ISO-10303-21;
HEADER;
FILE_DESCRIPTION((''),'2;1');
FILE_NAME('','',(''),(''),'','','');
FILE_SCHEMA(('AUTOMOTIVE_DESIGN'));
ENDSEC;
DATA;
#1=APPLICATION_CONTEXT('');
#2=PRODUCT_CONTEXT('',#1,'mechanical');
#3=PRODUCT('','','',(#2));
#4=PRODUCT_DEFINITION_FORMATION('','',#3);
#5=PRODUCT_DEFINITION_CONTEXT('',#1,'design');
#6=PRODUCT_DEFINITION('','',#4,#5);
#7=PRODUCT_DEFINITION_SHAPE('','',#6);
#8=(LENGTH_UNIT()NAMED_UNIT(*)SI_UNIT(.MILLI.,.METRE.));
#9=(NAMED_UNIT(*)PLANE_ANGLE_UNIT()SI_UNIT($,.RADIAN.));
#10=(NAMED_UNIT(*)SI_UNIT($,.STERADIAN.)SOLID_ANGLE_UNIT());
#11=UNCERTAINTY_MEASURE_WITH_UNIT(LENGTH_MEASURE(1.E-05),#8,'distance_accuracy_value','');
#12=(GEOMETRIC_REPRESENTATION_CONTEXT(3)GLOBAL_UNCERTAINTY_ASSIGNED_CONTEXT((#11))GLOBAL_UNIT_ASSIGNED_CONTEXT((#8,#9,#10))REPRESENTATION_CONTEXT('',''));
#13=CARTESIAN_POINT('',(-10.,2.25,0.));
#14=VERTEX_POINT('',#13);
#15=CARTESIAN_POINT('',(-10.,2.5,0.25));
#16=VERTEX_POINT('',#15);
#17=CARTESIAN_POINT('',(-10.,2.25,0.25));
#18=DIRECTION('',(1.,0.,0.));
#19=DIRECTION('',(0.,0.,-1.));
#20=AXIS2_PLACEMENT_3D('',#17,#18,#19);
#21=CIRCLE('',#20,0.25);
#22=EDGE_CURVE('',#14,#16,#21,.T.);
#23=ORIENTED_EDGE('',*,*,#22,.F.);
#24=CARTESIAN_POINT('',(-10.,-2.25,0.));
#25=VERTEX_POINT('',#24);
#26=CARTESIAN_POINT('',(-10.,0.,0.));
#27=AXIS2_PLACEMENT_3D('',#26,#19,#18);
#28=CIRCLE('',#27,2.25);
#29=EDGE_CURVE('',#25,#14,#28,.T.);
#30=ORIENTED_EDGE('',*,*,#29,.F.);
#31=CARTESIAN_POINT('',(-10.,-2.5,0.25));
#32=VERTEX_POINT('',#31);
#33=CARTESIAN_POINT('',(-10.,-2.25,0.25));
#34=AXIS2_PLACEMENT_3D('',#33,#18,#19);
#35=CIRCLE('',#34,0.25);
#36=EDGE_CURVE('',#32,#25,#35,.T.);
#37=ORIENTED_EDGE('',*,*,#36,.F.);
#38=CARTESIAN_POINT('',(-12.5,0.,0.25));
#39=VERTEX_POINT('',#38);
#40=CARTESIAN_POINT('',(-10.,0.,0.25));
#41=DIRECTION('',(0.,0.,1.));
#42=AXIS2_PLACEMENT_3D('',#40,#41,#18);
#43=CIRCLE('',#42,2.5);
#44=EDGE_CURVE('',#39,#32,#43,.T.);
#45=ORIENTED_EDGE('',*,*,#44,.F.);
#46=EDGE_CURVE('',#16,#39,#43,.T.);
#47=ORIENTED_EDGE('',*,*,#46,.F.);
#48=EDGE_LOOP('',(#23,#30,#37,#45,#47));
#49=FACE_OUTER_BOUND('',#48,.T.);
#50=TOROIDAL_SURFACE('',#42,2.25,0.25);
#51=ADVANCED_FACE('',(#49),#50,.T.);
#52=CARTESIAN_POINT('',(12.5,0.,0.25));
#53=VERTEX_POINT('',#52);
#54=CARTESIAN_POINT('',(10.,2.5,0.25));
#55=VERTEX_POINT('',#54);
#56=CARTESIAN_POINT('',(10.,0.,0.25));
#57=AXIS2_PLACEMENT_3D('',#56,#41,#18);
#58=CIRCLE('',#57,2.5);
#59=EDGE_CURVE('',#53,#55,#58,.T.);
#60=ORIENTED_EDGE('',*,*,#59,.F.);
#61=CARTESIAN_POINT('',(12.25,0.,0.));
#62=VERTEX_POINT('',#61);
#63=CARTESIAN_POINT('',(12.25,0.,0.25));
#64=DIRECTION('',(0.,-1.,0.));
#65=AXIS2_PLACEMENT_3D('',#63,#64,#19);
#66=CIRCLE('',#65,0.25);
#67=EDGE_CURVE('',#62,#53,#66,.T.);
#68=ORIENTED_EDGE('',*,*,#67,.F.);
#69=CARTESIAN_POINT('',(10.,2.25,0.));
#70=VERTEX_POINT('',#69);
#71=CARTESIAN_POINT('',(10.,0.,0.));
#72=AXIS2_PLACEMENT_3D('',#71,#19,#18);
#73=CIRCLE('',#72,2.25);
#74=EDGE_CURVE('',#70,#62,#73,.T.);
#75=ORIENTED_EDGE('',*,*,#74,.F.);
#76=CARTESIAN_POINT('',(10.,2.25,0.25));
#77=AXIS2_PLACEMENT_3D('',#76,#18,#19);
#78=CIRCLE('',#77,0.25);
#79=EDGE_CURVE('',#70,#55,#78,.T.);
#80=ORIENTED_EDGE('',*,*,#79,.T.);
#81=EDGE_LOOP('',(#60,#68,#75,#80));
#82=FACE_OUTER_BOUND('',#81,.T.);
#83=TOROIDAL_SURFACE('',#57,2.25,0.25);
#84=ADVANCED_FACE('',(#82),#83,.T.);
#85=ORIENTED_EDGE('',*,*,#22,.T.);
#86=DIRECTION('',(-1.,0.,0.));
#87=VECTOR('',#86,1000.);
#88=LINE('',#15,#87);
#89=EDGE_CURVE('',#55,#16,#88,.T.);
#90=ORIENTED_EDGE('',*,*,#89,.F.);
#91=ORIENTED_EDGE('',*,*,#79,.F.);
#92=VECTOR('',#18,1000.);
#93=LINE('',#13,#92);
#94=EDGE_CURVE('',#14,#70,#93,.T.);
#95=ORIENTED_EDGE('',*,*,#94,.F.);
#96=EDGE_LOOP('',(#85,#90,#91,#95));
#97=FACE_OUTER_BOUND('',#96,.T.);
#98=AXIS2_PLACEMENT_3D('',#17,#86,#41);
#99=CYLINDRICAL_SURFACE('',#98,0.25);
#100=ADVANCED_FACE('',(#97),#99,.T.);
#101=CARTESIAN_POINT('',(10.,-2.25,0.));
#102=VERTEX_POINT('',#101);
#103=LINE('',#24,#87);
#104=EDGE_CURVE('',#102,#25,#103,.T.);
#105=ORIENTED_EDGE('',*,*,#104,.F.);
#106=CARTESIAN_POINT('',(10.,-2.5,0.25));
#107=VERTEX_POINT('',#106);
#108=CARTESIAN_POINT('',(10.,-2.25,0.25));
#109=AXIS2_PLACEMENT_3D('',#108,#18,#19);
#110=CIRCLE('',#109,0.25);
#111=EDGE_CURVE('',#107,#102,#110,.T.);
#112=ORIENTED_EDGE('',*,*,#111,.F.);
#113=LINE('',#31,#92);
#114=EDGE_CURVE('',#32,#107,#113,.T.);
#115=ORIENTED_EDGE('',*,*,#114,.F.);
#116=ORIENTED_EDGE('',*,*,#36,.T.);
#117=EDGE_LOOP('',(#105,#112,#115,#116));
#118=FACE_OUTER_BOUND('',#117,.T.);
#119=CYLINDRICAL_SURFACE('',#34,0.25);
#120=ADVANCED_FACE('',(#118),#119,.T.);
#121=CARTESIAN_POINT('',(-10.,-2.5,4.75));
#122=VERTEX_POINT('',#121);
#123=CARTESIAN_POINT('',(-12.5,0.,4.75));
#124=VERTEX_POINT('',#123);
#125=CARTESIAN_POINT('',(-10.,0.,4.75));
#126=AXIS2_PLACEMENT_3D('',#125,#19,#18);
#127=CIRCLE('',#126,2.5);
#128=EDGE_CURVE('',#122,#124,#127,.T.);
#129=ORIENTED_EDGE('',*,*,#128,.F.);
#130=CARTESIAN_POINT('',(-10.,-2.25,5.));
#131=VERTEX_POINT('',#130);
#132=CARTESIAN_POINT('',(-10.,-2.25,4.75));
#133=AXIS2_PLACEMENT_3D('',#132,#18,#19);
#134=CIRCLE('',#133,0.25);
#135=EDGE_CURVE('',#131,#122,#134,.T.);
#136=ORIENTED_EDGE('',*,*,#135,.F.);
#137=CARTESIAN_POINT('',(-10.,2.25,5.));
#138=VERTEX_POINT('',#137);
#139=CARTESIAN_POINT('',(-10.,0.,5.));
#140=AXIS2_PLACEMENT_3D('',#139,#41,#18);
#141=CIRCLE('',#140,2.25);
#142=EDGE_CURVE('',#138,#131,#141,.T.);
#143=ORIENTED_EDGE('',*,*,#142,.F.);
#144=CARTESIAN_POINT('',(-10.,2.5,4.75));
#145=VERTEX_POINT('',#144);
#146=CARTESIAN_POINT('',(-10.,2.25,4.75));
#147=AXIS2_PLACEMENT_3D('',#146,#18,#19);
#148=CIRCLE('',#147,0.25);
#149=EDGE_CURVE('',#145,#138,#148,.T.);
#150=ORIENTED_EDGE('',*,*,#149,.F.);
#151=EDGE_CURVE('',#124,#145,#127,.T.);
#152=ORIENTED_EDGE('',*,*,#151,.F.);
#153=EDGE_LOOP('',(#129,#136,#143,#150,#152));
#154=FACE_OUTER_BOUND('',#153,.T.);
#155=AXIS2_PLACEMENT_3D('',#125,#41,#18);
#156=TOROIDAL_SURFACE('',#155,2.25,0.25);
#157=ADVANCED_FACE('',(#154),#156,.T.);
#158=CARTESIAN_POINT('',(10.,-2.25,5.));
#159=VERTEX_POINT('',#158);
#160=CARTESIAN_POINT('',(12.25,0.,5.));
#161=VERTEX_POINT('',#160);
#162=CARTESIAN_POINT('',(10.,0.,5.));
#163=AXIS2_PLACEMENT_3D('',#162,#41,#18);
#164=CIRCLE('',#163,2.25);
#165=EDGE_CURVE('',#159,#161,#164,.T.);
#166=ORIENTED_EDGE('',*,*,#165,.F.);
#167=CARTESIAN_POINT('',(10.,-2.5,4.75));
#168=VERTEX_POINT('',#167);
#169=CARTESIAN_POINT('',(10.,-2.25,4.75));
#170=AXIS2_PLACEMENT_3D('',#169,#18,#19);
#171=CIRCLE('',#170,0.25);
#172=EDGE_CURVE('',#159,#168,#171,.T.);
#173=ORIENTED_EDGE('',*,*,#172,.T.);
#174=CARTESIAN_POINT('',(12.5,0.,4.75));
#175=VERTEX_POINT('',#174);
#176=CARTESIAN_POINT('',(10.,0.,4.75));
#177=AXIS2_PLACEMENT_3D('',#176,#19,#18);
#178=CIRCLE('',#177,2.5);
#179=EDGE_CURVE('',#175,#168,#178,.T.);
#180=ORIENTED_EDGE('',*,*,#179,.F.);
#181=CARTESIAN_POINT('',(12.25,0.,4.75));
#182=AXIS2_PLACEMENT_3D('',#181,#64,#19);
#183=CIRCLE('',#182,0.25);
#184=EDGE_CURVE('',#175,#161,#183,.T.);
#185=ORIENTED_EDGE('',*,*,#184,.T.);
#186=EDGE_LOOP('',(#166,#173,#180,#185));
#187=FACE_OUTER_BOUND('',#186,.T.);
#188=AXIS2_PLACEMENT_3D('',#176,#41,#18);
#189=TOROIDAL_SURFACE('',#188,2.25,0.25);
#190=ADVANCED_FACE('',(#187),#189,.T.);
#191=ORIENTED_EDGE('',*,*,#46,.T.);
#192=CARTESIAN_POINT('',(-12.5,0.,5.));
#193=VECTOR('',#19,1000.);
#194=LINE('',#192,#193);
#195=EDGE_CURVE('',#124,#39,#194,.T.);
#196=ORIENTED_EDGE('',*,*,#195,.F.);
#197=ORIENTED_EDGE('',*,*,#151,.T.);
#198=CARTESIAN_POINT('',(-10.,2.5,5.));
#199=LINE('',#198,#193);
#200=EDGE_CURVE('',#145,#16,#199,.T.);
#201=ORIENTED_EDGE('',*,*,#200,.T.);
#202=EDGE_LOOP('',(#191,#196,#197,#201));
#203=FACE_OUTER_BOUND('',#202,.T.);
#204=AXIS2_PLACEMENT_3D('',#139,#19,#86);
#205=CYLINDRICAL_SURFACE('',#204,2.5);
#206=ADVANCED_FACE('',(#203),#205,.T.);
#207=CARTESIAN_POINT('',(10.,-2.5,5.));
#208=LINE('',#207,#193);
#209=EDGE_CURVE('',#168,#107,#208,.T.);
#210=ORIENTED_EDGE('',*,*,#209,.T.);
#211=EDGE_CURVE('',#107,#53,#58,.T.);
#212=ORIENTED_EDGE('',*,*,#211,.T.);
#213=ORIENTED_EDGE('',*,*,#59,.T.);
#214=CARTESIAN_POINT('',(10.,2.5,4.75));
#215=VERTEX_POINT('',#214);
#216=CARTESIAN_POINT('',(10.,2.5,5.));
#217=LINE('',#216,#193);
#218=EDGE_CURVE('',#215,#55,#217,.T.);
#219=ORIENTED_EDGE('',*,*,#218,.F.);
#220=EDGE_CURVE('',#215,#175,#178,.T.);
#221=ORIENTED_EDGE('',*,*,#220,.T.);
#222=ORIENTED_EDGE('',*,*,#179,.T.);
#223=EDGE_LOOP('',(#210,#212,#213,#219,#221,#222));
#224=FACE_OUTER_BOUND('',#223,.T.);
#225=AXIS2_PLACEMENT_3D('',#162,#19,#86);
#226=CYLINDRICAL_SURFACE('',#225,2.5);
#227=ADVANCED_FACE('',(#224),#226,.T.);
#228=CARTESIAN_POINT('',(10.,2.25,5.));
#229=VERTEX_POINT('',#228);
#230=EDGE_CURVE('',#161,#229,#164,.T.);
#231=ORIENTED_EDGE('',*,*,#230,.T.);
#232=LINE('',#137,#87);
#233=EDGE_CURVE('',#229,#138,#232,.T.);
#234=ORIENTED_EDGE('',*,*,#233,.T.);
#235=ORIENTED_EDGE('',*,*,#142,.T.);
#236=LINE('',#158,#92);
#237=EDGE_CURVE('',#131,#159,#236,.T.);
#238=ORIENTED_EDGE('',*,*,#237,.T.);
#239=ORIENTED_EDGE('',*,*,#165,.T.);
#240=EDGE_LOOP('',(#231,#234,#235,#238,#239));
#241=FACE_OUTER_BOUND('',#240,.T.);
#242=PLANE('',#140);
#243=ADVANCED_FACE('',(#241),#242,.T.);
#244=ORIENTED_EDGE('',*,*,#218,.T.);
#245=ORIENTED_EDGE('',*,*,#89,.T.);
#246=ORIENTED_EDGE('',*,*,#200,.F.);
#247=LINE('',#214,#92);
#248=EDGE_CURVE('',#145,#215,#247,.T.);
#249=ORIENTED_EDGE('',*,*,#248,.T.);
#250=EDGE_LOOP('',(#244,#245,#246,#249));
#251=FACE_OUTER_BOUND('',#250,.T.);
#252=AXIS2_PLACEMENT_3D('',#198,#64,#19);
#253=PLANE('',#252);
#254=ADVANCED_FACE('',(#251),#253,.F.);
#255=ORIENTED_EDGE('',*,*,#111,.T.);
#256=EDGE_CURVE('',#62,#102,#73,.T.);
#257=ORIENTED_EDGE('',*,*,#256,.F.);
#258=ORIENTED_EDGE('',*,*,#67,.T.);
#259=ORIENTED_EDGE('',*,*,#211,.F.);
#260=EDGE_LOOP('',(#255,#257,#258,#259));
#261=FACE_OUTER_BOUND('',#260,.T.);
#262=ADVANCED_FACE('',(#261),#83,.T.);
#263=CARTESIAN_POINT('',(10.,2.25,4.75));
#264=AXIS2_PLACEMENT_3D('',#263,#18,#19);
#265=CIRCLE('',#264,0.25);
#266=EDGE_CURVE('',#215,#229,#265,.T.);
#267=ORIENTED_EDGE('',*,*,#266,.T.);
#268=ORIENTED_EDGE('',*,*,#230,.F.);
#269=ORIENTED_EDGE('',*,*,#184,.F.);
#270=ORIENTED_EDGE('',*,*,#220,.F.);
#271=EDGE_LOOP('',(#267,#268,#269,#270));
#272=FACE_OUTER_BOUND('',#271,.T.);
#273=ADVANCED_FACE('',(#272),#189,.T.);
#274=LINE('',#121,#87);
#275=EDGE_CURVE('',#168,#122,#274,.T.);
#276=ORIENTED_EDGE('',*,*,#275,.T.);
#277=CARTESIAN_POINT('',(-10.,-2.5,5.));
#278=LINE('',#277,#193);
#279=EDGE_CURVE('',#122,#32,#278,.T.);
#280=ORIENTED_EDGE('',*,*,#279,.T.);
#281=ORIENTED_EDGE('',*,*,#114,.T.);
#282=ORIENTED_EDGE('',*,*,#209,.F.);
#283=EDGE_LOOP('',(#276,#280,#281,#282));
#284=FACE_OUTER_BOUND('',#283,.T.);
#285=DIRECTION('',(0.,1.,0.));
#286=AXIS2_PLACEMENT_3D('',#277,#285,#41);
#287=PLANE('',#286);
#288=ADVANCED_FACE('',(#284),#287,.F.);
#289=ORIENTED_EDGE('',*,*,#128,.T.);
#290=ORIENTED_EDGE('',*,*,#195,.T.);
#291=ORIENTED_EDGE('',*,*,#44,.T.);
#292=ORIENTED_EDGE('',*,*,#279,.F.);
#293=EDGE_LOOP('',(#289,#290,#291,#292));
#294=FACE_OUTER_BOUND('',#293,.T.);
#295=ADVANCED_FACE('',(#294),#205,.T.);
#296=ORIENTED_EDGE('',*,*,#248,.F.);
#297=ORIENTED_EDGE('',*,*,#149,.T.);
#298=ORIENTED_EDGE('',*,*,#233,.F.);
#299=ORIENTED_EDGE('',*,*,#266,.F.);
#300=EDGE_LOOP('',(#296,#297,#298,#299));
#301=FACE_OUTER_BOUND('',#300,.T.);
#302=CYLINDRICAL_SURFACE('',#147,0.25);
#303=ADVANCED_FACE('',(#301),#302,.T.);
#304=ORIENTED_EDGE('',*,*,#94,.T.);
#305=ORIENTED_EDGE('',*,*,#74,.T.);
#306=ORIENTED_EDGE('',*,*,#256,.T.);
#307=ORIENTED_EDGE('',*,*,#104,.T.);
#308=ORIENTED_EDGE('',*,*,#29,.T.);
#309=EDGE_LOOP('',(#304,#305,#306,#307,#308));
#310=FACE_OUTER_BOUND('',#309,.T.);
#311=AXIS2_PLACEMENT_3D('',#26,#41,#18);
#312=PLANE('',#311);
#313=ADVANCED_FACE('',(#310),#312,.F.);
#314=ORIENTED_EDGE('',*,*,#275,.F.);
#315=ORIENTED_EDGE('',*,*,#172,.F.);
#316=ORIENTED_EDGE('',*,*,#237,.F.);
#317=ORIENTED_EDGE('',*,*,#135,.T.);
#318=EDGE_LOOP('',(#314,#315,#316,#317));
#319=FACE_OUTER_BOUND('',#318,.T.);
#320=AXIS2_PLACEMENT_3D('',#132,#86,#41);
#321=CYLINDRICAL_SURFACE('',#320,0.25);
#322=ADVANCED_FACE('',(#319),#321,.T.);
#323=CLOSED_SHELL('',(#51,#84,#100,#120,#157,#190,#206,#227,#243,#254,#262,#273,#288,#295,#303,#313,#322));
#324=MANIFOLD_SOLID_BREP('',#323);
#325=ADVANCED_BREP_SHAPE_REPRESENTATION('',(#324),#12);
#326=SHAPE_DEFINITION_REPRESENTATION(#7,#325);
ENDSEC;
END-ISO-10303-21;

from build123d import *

# Parameters (mm, degrees)
BASE_EXTRUDE_DEPTH = 5
FILLET1_R          = 0.25


with BuildPart() as part:
    # Sketch1 → Base-Extrude (new body)
    with BuildSketch(Plane.XY):
        with BuildLine():
            Line((-10, 2.5), (10, 2.5))
            ThreePointArc((10, 2.5), (12.5, 0), (10, -2.5))
            Line((10, -2.5), (-10, -2.5))
            ThreePointArc((-10, -2.5), (-12.5, 0), (-10, 2.5))
        make_face()
    extrude(amount=BASE_EXTRUDE_DEPTH)

    # Fillet1
    fillet1_edges = [part.edges().sort_by_distance(p)[0] for p in [
        (12.5, 0, 5),
        (0, 2.5, 5),
        (-12.5, 0, 5),
        (0, 2.5, 0),
        (12.5, 0, 0),
        (0, -2.5, 0),
        (-12.5, 0, 0),
        (0, -2.5, 5),
    ]]
    fillet(fillet1_edges, radius=FILLET1_R)


solid = part.part
